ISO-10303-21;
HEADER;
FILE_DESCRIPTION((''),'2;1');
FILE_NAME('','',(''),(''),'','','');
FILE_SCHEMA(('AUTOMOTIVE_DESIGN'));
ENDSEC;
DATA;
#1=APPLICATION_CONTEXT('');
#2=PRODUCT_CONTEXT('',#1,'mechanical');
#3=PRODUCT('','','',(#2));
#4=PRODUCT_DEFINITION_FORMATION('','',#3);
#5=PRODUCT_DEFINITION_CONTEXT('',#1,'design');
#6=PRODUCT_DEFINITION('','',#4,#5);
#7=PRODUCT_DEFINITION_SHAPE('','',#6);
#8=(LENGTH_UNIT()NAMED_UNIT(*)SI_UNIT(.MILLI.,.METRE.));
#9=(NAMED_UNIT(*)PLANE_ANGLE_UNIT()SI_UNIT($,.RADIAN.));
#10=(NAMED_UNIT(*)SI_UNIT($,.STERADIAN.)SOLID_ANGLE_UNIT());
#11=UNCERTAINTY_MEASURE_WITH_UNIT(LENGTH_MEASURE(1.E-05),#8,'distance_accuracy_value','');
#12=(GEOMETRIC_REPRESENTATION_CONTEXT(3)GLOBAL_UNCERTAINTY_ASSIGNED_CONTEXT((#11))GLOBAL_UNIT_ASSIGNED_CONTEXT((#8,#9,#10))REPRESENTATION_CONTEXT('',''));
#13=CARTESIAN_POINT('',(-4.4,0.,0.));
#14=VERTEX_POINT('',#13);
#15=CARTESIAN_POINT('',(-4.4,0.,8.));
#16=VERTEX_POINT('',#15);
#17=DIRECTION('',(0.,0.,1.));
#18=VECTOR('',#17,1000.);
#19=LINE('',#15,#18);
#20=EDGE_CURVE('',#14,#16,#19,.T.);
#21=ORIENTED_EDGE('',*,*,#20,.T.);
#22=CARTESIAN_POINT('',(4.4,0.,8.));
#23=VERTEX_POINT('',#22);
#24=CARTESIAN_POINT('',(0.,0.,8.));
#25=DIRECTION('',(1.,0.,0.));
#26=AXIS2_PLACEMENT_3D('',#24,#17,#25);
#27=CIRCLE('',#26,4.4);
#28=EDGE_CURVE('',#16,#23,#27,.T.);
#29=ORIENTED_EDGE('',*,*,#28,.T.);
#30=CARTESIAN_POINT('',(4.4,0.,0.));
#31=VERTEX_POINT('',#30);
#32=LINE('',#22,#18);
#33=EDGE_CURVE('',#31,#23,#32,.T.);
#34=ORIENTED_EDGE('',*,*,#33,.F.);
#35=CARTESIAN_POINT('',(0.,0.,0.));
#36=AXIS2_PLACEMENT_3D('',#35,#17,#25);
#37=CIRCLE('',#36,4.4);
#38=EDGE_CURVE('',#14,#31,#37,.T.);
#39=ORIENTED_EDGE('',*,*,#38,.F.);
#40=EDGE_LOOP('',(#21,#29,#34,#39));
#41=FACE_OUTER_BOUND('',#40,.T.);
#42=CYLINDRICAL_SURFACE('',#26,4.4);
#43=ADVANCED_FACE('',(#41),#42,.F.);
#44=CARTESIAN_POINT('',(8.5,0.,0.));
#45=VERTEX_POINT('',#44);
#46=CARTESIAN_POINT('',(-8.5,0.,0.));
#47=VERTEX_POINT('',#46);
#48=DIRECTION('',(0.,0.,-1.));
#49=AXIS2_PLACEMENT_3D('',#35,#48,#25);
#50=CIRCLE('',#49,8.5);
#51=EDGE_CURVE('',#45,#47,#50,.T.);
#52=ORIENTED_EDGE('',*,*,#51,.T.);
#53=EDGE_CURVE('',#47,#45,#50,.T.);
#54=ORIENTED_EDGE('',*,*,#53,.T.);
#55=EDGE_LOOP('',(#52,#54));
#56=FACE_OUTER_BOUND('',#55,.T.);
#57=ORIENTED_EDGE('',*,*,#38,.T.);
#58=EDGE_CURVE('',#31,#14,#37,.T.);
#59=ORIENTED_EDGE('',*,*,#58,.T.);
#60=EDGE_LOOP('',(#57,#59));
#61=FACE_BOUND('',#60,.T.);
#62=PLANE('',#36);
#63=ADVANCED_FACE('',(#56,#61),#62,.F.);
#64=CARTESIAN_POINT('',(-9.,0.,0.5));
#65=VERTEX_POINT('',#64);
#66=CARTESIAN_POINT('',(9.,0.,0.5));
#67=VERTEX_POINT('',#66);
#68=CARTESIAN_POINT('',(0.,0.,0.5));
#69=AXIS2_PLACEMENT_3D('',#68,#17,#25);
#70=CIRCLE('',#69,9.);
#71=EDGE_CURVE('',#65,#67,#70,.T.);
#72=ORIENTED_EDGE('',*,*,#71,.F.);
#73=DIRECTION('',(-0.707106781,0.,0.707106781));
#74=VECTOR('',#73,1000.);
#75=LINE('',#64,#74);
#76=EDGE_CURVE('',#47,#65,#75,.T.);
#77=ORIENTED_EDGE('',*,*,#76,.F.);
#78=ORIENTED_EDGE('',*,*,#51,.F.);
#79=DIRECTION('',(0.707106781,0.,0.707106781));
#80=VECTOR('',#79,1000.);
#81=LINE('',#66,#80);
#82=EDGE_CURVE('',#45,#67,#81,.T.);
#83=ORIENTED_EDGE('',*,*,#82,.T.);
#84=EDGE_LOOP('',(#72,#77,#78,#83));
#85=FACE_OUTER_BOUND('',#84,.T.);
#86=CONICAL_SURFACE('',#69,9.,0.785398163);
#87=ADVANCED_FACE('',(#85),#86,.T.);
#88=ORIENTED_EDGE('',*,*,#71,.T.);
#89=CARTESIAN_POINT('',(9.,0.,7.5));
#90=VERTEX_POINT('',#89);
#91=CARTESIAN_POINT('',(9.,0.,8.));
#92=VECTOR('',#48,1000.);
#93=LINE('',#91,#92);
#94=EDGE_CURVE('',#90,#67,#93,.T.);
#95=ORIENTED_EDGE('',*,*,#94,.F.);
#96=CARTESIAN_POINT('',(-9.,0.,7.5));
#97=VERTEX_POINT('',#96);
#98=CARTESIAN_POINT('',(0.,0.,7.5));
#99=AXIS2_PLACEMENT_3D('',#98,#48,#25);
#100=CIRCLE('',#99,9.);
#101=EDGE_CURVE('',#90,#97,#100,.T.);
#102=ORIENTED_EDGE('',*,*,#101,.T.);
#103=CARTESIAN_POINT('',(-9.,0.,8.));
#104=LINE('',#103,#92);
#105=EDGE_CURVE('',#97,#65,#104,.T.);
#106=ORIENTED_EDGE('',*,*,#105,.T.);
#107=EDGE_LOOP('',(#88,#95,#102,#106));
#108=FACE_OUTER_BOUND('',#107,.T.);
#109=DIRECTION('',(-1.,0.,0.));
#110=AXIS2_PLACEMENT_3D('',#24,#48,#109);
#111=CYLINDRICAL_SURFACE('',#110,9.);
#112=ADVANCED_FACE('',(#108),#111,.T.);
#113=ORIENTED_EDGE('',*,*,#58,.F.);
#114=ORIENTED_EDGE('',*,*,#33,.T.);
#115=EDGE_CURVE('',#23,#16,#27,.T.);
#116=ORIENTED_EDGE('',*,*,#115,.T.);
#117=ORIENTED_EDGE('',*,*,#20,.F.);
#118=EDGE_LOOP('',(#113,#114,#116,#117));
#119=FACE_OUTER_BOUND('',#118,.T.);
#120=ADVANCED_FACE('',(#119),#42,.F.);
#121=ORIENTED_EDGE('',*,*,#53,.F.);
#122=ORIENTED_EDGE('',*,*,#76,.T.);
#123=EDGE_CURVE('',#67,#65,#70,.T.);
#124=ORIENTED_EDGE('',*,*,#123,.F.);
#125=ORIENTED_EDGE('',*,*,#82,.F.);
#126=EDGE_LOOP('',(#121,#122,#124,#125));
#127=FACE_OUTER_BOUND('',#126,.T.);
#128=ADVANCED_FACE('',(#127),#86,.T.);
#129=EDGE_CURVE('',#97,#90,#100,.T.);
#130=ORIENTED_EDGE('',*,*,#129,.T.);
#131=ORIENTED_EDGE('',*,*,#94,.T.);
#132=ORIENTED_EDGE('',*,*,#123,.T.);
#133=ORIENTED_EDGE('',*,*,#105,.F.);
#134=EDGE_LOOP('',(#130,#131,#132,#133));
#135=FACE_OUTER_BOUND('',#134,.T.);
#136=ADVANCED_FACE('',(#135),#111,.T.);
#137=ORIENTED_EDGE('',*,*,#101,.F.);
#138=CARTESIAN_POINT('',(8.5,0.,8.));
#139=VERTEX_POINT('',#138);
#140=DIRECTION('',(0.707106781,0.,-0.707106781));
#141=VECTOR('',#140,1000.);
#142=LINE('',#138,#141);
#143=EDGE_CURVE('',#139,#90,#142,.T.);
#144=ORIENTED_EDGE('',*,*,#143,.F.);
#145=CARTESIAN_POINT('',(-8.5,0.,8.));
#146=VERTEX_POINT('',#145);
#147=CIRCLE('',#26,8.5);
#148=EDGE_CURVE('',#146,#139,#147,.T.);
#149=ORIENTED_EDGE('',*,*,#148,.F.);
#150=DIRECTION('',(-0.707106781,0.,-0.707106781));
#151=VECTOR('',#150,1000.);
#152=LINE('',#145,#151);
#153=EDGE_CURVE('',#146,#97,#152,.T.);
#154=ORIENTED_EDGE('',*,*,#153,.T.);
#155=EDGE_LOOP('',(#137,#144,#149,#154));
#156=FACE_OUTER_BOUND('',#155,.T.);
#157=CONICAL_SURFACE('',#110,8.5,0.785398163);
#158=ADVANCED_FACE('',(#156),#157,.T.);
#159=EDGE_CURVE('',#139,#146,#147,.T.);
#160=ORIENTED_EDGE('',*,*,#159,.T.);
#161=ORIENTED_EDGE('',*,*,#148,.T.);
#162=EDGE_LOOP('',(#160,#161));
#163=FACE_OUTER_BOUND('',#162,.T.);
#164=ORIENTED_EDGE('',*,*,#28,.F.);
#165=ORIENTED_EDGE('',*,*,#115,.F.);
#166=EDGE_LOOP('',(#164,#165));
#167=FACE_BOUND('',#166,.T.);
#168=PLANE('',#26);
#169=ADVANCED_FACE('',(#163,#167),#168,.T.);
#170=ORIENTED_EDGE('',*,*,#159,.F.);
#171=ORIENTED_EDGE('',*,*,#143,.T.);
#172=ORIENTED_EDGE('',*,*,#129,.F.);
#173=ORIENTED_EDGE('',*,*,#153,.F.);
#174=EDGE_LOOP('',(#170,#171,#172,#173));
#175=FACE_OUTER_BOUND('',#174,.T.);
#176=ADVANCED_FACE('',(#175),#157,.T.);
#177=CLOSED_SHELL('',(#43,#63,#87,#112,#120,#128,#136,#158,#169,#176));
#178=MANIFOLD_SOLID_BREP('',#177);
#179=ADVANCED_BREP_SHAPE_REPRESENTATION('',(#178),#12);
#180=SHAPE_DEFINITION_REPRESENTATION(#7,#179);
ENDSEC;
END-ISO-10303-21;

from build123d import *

# Parameters (mm, degrees)
SKETCH_1_R           = 9
EXTRUDE_1_DEPTH      = 8
HOLE_WIZARD_G1_8_1_D = 8.8
CHAMFER_1_SIZE       = 0.5


with BuildPart() as part:
    # 草图1 → 凸台-拉伸1 (new body)
    with BuildSketch(Plane.XY):
        Circle(SKETCH_1_R)
    extrude(amount=EXTRUDE_1_DEPTH)

    # G1/8 螺纹孔1 (through all)
    with Locations(Plane.XY.offset(8)):
        with Locations((0, 0)):
            Hole(HOLE_WIZARD_G1_8_1_D / 2)

    # 倒角1
    chamfer_1_edges = [part.edges().sort_by_distance(p)[0] for p in [
        (-9, 0, 0),
        (-9, 0, 8),
    ]]
    chamfer(chamfer_1_edges, length=CHAMFER_1_SIZE)


solid = part.part
